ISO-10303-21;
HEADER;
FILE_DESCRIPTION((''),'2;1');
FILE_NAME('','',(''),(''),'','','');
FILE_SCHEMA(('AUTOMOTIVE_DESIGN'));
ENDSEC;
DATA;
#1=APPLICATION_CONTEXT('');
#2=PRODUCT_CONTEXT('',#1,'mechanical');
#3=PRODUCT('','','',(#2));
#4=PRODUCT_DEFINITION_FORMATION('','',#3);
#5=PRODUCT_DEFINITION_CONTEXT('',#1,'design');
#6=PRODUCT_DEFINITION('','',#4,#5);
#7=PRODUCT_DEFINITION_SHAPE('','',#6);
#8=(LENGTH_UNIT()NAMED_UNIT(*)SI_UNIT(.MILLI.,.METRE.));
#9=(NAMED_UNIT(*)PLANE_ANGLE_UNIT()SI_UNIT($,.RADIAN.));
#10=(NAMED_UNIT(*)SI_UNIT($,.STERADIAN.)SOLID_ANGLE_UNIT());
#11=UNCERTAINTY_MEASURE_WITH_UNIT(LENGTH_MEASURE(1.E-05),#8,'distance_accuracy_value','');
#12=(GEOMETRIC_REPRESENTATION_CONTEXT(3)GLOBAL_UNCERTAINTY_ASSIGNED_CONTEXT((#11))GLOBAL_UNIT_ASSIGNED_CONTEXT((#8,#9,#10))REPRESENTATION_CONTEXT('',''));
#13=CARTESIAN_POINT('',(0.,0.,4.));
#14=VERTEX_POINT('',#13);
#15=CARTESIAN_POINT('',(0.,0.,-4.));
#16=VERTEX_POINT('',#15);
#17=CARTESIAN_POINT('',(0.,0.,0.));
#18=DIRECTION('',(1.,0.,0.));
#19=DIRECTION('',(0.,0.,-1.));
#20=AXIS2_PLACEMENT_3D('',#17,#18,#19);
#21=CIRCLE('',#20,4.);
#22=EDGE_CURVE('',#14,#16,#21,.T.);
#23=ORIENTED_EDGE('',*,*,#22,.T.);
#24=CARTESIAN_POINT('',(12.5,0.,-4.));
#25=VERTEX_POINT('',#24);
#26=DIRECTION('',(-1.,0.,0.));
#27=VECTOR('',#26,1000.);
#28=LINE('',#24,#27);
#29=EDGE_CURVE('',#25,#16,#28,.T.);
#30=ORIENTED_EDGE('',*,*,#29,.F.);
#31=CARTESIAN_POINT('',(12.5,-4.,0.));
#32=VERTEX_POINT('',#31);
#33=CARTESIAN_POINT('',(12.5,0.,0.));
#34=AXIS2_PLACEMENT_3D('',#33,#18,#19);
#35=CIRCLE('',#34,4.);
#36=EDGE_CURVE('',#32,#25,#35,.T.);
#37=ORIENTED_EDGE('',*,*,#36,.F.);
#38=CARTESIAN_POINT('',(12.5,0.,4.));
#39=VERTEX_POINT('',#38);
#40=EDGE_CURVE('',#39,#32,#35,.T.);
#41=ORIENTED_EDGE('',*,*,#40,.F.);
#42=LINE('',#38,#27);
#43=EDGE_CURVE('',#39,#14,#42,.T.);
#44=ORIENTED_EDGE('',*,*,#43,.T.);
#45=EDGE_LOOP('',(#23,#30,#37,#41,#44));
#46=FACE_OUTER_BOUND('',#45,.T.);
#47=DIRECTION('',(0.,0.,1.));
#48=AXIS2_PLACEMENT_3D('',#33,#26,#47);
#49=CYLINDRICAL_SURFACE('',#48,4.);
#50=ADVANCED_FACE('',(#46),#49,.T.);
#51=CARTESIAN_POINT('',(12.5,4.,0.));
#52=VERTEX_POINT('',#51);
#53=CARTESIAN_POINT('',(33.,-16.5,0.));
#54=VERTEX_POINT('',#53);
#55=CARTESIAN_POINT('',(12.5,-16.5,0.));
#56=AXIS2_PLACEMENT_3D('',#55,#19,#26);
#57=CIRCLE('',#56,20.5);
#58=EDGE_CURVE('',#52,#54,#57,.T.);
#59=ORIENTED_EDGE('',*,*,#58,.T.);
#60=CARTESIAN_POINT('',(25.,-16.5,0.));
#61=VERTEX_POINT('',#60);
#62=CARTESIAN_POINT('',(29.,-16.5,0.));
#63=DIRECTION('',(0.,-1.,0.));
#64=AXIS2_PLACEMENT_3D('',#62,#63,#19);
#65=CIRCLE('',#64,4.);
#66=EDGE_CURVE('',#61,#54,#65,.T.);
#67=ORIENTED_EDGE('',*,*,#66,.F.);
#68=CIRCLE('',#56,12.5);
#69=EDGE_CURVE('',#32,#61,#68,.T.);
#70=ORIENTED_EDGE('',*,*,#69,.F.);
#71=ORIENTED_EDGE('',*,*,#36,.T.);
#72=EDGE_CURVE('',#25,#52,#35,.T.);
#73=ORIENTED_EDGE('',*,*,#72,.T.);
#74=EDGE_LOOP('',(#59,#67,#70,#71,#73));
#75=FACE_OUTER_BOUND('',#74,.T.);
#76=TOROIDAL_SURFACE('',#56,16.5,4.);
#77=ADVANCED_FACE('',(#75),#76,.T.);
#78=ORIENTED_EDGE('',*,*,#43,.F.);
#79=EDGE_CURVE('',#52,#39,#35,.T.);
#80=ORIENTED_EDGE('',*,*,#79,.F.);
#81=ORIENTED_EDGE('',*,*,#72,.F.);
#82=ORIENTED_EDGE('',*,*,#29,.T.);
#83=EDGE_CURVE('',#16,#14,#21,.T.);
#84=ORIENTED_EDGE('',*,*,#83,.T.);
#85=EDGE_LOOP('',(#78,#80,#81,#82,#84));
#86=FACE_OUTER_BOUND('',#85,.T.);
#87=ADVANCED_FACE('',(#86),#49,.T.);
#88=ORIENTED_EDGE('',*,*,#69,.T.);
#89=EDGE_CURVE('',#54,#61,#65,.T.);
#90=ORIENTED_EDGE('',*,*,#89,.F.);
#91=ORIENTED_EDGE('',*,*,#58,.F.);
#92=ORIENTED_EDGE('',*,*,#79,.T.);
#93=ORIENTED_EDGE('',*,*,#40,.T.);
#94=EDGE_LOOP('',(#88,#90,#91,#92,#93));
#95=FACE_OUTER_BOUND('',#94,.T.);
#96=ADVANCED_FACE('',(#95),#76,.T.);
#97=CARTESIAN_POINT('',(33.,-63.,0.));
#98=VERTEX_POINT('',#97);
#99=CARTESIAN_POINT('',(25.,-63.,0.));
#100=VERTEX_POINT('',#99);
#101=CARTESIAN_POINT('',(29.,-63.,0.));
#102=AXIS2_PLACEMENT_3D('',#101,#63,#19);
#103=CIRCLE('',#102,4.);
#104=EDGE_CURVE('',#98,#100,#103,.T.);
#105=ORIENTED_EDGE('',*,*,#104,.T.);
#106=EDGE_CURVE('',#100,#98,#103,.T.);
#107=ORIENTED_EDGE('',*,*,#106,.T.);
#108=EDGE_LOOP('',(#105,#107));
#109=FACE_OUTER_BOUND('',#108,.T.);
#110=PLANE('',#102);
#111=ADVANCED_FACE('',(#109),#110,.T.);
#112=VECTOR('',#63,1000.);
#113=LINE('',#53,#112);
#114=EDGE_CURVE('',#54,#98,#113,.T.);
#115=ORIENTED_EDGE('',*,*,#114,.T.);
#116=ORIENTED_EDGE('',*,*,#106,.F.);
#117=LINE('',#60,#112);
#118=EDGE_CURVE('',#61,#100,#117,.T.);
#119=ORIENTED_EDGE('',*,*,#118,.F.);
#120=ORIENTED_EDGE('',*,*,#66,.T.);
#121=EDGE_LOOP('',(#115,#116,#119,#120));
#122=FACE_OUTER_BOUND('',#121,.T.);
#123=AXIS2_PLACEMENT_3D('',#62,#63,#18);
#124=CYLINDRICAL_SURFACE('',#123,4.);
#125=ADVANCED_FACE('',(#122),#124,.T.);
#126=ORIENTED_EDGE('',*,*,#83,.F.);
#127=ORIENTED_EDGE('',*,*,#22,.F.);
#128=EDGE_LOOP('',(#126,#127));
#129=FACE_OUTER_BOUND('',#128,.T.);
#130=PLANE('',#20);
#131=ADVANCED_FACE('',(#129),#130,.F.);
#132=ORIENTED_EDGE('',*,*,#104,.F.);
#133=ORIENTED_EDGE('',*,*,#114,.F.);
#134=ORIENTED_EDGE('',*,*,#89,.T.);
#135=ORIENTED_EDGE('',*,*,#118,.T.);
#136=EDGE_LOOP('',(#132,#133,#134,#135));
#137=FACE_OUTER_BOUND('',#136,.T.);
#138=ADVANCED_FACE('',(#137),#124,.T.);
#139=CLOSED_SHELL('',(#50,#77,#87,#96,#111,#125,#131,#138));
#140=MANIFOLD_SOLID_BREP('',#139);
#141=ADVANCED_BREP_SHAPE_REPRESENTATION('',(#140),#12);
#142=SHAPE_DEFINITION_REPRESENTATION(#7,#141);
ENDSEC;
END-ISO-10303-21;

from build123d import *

# Parameters (mm, degrees)
SKETCH2_R = 4


with BuildPart() as part:
    # Sweep1: sweep along a path in Sketch1
    with BuildLine(Plane.XY) as sweep1_path:
        Line((0, 0), (12.5, 0))
        ThreePointArc((12.5, 0), (24.16726189, -4.83273811), (29, -16.5))
        Line((29, -16.5), (29, -63))
    # Sketch2 → Sweep1 (sweep)
    with BuildSketch(Plane(origin=(0, 0, 0), x_dir=(0, 0, -1), z_dir=(1, 0, 0))):
        Circle(SKETCH2_R)
    sweep(path=sweep1_path.line)


solid = part.part
